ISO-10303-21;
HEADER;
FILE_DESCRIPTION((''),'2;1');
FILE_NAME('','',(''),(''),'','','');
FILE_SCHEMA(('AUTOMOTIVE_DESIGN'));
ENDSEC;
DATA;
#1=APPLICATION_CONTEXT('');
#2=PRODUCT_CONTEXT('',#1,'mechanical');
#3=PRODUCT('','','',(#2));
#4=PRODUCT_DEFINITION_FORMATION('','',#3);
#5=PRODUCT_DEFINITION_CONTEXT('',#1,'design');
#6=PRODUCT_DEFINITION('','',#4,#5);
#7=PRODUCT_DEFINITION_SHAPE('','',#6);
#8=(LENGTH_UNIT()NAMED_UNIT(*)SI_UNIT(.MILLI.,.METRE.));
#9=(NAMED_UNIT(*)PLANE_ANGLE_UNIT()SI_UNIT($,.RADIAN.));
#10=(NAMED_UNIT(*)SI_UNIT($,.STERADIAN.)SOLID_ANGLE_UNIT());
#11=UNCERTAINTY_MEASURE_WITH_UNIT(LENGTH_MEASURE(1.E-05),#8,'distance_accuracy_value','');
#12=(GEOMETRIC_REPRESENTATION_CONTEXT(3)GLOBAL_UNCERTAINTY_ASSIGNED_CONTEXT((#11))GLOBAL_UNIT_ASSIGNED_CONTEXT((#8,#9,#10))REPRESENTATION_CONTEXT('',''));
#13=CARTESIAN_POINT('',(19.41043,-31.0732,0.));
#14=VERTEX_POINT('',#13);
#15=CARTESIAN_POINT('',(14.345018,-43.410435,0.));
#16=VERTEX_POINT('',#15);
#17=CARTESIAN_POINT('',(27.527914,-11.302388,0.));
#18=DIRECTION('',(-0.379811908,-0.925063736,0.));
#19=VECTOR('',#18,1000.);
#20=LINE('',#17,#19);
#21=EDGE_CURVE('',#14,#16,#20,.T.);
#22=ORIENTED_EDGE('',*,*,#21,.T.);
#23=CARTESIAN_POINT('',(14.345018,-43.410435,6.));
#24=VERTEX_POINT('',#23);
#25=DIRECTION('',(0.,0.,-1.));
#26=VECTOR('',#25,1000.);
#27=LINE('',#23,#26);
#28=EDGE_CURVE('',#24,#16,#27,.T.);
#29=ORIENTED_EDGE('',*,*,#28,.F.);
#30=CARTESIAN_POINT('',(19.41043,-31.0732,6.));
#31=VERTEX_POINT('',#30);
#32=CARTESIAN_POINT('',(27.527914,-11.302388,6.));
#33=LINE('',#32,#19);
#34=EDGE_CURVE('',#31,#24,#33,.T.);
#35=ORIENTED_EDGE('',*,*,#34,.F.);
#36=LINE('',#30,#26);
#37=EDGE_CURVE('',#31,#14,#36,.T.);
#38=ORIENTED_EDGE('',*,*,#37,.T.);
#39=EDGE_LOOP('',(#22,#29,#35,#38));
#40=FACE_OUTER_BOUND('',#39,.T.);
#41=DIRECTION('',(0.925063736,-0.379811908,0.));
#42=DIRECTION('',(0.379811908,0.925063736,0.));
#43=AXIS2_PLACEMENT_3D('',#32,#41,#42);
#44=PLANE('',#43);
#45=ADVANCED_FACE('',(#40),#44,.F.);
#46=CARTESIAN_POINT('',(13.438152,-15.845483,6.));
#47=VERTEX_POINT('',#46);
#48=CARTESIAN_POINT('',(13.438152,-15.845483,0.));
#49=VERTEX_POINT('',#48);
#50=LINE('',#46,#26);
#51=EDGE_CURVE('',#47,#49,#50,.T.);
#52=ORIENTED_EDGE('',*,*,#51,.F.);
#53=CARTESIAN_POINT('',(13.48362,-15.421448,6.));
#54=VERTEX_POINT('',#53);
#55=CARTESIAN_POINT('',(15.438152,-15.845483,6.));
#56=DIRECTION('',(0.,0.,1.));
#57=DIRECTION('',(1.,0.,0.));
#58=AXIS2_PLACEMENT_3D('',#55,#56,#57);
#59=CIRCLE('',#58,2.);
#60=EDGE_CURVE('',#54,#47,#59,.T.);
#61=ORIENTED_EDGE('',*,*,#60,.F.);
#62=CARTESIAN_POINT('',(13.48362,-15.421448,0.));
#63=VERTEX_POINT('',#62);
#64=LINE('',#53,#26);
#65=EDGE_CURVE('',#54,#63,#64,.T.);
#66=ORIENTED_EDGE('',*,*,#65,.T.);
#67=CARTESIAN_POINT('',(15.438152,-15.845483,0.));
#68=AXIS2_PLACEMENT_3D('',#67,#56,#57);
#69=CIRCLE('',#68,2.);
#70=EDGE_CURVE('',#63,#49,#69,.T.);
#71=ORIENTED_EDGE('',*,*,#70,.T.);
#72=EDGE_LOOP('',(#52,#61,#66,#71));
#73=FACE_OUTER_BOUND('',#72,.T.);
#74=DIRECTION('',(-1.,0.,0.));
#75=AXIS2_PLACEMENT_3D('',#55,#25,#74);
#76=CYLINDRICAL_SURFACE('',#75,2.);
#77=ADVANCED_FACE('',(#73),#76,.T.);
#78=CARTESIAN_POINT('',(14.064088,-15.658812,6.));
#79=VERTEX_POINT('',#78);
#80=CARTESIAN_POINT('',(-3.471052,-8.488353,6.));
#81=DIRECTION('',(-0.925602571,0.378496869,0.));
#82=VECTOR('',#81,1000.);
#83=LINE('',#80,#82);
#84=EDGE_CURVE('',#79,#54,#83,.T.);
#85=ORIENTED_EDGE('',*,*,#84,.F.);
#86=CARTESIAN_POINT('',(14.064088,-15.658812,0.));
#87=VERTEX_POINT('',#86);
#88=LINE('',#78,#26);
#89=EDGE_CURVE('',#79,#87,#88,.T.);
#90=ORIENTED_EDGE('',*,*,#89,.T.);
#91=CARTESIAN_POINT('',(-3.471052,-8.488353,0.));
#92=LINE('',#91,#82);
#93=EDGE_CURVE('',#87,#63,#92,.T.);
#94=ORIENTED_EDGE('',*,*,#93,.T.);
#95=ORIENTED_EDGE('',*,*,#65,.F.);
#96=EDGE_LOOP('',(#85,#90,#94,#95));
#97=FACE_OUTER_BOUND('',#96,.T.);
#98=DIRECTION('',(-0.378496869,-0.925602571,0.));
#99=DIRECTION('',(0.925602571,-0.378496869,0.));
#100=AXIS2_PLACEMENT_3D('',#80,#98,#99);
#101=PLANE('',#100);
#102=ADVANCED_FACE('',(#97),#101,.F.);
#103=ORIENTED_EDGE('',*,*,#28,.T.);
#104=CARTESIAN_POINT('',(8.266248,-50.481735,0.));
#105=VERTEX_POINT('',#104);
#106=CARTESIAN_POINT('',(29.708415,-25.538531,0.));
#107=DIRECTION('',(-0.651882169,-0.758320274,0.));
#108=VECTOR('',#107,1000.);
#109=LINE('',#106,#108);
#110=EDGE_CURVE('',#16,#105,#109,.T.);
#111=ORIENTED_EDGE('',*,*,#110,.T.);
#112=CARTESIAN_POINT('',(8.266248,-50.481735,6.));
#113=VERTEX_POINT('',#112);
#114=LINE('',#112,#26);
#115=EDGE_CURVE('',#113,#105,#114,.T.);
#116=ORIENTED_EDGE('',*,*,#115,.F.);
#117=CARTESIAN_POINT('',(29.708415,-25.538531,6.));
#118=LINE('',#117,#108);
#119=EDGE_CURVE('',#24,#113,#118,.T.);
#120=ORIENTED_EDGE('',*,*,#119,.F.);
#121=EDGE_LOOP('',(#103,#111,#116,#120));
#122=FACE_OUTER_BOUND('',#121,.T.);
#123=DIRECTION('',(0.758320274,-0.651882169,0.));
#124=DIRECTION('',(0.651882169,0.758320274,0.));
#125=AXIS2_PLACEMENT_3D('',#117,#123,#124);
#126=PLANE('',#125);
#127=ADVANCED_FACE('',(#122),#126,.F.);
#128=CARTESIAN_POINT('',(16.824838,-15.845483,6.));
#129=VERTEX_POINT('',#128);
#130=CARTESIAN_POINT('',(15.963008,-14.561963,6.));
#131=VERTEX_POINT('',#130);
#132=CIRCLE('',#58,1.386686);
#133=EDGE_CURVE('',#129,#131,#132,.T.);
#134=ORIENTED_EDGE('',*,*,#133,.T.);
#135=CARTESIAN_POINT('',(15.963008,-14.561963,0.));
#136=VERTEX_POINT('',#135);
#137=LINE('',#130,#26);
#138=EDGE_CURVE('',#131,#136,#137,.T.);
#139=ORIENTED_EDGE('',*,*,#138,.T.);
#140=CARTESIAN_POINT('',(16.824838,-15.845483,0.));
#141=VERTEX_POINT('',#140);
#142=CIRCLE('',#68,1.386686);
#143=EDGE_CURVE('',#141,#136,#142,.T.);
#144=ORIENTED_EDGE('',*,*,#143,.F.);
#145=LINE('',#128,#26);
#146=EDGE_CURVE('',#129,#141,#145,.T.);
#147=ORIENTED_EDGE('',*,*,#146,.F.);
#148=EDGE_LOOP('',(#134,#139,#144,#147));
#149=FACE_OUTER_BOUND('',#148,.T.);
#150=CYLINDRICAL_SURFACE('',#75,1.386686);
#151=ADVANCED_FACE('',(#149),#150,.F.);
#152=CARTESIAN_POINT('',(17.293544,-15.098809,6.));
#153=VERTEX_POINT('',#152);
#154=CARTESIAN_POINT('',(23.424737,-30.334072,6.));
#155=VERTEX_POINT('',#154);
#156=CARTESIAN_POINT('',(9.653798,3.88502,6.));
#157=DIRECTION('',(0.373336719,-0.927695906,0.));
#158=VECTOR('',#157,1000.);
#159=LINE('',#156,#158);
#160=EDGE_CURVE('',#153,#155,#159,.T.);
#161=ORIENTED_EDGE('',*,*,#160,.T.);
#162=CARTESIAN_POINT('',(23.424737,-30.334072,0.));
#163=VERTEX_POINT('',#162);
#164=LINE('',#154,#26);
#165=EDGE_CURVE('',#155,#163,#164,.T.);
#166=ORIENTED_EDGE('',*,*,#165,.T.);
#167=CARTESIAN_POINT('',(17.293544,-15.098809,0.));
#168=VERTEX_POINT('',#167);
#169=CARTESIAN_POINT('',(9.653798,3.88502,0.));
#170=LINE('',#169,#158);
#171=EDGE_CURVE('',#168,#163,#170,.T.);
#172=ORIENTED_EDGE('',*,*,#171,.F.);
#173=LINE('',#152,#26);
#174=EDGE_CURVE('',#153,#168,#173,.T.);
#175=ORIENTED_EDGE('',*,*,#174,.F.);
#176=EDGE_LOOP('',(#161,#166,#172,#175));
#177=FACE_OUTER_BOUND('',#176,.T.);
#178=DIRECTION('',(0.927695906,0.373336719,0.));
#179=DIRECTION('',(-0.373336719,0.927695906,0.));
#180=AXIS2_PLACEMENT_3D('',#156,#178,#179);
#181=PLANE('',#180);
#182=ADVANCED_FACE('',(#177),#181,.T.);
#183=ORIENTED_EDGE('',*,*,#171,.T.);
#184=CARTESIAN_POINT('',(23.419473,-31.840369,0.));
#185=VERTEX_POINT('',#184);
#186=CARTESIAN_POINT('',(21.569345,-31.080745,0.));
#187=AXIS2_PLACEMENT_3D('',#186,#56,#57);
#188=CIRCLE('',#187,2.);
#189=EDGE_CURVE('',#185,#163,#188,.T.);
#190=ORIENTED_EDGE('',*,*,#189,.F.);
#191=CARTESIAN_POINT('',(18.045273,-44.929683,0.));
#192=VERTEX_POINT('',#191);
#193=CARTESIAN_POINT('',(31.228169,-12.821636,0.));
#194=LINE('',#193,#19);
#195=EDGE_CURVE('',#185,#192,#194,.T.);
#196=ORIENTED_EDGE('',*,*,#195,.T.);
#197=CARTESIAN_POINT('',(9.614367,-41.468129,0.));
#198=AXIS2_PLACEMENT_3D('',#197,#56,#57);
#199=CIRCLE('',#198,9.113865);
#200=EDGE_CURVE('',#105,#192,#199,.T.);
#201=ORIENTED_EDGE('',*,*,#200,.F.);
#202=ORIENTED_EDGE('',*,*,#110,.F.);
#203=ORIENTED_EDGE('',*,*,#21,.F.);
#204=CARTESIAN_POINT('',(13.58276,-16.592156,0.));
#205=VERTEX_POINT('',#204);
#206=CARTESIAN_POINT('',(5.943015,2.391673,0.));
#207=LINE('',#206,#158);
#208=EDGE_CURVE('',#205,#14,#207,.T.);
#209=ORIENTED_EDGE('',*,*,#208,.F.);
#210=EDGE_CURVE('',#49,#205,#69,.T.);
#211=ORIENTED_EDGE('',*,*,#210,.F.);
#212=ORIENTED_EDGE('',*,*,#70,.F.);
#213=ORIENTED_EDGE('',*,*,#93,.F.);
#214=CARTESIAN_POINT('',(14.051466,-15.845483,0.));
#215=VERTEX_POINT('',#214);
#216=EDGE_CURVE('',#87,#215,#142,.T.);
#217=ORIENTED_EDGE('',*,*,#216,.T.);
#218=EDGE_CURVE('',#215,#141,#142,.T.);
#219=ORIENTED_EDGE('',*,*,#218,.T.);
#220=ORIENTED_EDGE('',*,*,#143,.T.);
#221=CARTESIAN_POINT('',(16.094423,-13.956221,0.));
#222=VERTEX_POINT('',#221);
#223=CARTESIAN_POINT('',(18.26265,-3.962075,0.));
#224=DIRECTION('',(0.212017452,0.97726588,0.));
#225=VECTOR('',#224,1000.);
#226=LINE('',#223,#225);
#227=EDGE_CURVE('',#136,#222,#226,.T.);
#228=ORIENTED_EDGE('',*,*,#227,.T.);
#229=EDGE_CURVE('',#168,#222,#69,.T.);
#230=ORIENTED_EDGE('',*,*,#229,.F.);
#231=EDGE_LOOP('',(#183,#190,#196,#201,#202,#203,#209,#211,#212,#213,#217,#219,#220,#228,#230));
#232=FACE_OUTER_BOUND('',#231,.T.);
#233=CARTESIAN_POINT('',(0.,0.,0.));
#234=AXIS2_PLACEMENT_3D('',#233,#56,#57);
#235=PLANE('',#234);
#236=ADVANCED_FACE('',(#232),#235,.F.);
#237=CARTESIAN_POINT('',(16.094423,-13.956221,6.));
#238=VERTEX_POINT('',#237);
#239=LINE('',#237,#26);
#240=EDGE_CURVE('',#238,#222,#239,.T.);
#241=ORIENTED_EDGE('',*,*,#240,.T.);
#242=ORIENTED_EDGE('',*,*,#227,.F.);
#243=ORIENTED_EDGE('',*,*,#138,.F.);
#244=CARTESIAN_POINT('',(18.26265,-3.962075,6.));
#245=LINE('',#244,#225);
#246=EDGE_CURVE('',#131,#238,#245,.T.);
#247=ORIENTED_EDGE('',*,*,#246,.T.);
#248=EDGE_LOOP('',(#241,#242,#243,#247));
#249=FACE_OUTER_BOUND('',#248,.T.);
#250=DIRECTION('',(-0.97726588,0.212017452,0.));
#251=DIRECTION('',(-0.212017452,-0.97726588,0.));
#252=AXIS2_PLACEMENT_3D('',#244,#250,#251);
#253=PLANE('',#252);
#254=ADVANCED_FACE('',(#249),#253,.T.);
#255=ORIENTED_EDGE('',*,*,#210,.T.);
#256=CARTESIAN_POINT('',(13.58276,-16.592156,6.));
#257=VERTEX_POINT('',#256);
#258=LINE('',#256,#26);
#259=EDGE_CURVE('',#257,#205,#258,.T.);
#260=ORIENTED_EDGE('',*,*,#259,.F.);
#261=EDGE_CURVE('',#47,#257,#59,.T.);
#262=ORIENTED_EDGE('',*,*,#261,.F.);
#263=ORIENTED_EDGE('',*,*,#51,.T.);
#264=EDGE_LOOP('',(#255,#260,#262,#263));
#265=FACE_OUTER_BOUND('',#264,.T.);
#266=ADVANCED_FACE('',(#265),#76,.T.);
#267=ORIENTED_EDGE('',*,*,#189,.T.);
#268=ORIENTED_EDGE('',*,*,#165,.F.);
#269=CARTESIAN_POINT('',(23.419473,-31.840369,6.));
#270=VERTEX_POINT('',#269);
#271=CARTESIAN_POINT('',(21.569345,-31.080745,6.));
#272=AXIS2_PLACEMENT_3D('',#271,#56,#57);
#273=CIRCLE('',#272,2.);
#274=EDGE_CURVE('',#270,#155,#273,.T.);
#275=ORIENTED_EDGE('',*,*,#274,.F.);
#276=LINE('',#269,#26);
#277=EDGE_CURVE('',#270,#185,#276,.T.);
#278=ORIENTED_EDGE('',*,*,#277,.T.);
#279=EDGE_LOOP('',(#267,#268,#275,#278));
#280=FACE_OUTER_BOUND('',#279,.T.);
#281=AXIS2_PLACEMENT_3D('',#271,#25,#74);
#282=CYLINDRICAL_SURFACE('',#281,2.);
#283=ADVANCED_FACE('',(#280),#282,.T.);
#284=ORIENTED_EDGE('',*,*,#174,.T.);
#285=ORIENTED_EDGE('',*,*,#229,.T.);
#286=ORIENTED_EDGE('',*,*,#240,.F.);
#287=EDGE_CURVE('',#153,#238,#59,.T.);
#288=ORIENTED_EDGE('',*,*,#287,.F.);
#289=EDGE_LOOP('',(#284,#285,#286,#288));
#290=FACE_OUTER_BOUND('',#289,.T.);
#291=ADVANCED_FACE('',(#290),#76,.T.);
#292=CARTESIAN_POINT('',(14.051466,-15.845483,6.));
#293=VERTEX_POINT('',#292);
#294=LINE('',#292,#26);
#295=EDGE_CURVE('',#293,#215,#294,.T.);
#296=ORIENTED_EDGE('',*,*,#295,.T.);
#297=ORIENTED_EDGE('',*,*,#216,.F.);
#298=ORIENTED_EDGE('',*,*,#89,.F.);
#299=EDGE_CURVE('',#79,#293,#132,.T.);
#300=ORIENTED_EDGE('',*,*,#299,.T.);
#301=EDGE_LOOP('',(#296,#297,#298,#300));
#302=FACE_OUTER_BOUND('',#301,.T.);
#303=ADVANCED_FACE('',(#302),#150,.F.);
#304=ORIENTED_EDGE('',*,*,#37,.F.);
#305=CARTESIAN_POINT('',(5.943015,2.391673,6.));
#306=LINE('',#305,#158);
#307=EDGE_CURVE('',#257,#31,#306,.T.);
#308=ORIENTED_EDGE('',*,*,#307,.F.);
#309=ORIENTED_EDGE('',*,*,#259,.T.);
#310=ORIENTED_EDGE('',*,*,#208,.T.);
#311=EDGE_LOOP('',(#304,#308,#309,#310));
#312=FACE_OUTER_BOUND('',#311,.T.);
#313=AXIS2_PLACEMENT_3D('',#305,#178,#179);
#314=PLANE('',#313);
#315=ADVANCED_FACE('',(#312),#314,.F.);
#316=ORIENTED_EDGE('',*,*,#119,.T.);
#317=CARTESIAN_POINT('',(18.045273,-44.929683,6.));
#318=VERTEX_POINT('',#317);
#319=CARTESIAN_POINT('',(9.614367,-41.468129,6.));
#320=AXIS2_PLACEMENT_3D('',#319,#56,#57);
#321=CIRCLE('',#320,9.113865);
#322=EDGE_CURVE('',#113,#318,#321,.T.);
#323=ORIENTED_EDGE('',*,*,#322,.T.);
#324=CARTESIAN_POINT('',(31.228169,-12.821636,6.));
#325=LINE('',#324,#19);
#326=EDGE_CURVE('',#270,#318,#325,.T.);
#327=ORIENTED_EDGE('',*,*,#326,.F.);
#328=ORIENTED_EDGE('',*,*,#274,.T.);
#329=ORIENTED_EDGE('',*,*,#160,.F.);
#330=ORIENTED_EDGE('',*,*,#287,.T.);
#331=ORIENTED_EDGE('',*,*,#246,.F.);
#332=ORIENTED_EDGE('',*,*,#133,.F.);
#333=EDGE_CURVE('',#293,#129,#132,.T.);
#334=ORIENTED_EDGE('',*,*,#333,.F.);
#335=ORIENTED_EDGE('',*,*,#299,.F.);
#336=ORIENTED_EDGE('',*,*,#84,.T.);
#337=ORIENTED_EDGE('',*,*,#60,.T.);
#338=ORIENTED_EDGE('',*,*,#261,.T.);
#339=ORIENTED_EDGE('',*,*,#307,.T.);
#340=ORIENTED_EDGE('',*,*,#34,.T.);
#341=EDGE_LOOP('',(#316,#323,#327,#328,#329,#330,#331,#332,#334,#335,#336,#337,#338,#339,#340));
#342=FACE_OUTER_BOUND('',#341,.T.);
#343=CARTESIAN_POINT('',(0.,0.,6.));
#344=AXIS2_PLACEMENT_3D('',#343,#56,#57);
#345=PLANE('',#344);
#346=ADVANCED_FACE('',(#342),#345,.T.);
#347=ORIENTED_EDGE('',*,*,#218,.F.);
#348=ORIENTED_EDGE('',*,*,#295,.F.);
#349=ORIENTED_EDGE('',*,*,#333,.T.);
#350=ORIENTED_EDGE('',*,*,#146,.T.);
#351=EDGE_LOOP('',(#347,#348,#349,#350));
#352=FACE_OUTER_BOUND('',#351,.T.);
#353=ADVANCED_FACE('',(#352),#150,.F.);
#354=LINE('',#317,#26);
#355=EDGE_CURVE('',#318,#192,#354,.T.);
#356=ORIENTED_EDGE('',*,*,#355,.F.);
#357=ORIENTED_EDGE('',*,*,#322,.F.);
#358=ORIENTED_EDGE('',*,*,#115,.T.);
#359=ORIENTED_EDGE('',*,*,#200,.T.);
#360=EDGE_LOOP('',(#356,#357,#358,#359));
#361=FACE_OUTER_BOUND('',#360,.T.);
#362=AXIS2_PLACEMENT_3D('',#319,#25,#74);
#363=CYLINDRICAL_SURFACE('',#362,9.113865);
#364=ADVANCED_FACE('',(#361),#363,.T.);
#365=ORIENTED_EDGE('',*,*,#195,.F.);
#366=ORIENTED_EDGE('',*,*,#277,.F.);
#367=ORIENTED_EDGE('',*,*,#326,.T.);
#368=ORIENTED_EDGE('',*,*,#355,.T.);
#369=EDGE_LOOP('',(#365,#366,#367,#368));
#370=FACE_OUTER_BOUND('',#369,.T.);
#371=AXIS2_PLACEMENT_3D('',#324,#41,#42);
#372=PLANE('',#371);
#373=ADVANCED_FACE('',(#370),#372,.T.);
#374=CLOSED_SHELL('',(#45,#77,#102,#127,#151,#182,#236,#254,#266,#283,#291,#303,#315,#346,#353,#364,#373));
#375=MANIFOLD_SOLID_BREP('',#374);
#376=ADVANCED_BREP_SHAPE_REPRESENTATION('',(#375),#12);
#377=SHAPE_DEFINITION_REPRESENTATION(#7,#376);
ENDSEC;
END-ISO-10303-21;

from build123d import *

# Parameters (mm, degrees)
BOSS_EXTRUDE1_DEPTH = 6


with BuildPart() as part:
    # Sketch1 → Boss-Extrude1 (new body)
    with BuildSketch(Plane.XY):
        with BuildLine():
            Line((23.424737155, -30.334071959), (17.293543757, -15.098809177))
            ThreePointArc((17.293543757, -15.098809177), (16.817822135, -14.397549548), (16.094423456, -13.956221462))
            Line((16.094423456, -13.956221462), (15.963008089, -14.561962892))
            ThreePointArc((15.963008089, -14.561962892), (16.131735441, -17.04624853), (14.064088238, -15.658812373))
            Line((14.064088238, -15.658812373), (13.483620184, -15.421447711))
            ThreePointArc((13.483620184, -15.421447711), (13.445284936, -16.014246024), (13.582760132, -16.592156052))
            Line((13.582760132, -16.592156052), (19.41043004, -31.073200227))
            Line((19.41043004, -31.073200227), (19.719217872, -30.321121581))
            ThreePointArc((19.719217872, -30.321121581), (21.576335078, -29.08075761), (23.424737155, -30.334071959))
        make_face()
        with BuildLine():
            ThreePointArc((23.419472814, -31.840369211), (23.569333129, -31.087735131), (23.424737155, -30.334071959))
            ThreePointArc((23.424737155, -30.334071959), (21.576335078, -29.08075761), (19.719217872, -30.321121581))
            Line((19.719217872, -30.321121581), (19.41043004, -31.073200227))
            Line((19.41043004, -31.073200227), (19.71395353, -31.827418834))
            ThreePointArc((19.71395353, -31.827418834), (21.562355608, -33.080733182), (23.419472814, -31.840369211))
        make_face()
        with BuildLine():
            Line((18.045273154, -44.929682928), (23.419472814, -31.840369211))
            ThreePointArc((23.419472814, -31.840369211), (21.562355608, -33.080733182), (19.71395353, -31.827418834))
            Line((19.71395353, -31.827418834), (19.41043004, -31.073200227))
            Line((19.41043004, -31.073200227), (14.345018212, -43.410435298))
            Line((14.345018212, -43.410435298), (8.266248414, -50.481735298))
            ThreePointArc((8.266248414, -50.481735298), (14.114121661, -49.393703769), (18.045273154, -44.929682928))
        make_face()
    extrude(amount=BOSS_EXTRUDE1_DEPTH)


solid = part.part
